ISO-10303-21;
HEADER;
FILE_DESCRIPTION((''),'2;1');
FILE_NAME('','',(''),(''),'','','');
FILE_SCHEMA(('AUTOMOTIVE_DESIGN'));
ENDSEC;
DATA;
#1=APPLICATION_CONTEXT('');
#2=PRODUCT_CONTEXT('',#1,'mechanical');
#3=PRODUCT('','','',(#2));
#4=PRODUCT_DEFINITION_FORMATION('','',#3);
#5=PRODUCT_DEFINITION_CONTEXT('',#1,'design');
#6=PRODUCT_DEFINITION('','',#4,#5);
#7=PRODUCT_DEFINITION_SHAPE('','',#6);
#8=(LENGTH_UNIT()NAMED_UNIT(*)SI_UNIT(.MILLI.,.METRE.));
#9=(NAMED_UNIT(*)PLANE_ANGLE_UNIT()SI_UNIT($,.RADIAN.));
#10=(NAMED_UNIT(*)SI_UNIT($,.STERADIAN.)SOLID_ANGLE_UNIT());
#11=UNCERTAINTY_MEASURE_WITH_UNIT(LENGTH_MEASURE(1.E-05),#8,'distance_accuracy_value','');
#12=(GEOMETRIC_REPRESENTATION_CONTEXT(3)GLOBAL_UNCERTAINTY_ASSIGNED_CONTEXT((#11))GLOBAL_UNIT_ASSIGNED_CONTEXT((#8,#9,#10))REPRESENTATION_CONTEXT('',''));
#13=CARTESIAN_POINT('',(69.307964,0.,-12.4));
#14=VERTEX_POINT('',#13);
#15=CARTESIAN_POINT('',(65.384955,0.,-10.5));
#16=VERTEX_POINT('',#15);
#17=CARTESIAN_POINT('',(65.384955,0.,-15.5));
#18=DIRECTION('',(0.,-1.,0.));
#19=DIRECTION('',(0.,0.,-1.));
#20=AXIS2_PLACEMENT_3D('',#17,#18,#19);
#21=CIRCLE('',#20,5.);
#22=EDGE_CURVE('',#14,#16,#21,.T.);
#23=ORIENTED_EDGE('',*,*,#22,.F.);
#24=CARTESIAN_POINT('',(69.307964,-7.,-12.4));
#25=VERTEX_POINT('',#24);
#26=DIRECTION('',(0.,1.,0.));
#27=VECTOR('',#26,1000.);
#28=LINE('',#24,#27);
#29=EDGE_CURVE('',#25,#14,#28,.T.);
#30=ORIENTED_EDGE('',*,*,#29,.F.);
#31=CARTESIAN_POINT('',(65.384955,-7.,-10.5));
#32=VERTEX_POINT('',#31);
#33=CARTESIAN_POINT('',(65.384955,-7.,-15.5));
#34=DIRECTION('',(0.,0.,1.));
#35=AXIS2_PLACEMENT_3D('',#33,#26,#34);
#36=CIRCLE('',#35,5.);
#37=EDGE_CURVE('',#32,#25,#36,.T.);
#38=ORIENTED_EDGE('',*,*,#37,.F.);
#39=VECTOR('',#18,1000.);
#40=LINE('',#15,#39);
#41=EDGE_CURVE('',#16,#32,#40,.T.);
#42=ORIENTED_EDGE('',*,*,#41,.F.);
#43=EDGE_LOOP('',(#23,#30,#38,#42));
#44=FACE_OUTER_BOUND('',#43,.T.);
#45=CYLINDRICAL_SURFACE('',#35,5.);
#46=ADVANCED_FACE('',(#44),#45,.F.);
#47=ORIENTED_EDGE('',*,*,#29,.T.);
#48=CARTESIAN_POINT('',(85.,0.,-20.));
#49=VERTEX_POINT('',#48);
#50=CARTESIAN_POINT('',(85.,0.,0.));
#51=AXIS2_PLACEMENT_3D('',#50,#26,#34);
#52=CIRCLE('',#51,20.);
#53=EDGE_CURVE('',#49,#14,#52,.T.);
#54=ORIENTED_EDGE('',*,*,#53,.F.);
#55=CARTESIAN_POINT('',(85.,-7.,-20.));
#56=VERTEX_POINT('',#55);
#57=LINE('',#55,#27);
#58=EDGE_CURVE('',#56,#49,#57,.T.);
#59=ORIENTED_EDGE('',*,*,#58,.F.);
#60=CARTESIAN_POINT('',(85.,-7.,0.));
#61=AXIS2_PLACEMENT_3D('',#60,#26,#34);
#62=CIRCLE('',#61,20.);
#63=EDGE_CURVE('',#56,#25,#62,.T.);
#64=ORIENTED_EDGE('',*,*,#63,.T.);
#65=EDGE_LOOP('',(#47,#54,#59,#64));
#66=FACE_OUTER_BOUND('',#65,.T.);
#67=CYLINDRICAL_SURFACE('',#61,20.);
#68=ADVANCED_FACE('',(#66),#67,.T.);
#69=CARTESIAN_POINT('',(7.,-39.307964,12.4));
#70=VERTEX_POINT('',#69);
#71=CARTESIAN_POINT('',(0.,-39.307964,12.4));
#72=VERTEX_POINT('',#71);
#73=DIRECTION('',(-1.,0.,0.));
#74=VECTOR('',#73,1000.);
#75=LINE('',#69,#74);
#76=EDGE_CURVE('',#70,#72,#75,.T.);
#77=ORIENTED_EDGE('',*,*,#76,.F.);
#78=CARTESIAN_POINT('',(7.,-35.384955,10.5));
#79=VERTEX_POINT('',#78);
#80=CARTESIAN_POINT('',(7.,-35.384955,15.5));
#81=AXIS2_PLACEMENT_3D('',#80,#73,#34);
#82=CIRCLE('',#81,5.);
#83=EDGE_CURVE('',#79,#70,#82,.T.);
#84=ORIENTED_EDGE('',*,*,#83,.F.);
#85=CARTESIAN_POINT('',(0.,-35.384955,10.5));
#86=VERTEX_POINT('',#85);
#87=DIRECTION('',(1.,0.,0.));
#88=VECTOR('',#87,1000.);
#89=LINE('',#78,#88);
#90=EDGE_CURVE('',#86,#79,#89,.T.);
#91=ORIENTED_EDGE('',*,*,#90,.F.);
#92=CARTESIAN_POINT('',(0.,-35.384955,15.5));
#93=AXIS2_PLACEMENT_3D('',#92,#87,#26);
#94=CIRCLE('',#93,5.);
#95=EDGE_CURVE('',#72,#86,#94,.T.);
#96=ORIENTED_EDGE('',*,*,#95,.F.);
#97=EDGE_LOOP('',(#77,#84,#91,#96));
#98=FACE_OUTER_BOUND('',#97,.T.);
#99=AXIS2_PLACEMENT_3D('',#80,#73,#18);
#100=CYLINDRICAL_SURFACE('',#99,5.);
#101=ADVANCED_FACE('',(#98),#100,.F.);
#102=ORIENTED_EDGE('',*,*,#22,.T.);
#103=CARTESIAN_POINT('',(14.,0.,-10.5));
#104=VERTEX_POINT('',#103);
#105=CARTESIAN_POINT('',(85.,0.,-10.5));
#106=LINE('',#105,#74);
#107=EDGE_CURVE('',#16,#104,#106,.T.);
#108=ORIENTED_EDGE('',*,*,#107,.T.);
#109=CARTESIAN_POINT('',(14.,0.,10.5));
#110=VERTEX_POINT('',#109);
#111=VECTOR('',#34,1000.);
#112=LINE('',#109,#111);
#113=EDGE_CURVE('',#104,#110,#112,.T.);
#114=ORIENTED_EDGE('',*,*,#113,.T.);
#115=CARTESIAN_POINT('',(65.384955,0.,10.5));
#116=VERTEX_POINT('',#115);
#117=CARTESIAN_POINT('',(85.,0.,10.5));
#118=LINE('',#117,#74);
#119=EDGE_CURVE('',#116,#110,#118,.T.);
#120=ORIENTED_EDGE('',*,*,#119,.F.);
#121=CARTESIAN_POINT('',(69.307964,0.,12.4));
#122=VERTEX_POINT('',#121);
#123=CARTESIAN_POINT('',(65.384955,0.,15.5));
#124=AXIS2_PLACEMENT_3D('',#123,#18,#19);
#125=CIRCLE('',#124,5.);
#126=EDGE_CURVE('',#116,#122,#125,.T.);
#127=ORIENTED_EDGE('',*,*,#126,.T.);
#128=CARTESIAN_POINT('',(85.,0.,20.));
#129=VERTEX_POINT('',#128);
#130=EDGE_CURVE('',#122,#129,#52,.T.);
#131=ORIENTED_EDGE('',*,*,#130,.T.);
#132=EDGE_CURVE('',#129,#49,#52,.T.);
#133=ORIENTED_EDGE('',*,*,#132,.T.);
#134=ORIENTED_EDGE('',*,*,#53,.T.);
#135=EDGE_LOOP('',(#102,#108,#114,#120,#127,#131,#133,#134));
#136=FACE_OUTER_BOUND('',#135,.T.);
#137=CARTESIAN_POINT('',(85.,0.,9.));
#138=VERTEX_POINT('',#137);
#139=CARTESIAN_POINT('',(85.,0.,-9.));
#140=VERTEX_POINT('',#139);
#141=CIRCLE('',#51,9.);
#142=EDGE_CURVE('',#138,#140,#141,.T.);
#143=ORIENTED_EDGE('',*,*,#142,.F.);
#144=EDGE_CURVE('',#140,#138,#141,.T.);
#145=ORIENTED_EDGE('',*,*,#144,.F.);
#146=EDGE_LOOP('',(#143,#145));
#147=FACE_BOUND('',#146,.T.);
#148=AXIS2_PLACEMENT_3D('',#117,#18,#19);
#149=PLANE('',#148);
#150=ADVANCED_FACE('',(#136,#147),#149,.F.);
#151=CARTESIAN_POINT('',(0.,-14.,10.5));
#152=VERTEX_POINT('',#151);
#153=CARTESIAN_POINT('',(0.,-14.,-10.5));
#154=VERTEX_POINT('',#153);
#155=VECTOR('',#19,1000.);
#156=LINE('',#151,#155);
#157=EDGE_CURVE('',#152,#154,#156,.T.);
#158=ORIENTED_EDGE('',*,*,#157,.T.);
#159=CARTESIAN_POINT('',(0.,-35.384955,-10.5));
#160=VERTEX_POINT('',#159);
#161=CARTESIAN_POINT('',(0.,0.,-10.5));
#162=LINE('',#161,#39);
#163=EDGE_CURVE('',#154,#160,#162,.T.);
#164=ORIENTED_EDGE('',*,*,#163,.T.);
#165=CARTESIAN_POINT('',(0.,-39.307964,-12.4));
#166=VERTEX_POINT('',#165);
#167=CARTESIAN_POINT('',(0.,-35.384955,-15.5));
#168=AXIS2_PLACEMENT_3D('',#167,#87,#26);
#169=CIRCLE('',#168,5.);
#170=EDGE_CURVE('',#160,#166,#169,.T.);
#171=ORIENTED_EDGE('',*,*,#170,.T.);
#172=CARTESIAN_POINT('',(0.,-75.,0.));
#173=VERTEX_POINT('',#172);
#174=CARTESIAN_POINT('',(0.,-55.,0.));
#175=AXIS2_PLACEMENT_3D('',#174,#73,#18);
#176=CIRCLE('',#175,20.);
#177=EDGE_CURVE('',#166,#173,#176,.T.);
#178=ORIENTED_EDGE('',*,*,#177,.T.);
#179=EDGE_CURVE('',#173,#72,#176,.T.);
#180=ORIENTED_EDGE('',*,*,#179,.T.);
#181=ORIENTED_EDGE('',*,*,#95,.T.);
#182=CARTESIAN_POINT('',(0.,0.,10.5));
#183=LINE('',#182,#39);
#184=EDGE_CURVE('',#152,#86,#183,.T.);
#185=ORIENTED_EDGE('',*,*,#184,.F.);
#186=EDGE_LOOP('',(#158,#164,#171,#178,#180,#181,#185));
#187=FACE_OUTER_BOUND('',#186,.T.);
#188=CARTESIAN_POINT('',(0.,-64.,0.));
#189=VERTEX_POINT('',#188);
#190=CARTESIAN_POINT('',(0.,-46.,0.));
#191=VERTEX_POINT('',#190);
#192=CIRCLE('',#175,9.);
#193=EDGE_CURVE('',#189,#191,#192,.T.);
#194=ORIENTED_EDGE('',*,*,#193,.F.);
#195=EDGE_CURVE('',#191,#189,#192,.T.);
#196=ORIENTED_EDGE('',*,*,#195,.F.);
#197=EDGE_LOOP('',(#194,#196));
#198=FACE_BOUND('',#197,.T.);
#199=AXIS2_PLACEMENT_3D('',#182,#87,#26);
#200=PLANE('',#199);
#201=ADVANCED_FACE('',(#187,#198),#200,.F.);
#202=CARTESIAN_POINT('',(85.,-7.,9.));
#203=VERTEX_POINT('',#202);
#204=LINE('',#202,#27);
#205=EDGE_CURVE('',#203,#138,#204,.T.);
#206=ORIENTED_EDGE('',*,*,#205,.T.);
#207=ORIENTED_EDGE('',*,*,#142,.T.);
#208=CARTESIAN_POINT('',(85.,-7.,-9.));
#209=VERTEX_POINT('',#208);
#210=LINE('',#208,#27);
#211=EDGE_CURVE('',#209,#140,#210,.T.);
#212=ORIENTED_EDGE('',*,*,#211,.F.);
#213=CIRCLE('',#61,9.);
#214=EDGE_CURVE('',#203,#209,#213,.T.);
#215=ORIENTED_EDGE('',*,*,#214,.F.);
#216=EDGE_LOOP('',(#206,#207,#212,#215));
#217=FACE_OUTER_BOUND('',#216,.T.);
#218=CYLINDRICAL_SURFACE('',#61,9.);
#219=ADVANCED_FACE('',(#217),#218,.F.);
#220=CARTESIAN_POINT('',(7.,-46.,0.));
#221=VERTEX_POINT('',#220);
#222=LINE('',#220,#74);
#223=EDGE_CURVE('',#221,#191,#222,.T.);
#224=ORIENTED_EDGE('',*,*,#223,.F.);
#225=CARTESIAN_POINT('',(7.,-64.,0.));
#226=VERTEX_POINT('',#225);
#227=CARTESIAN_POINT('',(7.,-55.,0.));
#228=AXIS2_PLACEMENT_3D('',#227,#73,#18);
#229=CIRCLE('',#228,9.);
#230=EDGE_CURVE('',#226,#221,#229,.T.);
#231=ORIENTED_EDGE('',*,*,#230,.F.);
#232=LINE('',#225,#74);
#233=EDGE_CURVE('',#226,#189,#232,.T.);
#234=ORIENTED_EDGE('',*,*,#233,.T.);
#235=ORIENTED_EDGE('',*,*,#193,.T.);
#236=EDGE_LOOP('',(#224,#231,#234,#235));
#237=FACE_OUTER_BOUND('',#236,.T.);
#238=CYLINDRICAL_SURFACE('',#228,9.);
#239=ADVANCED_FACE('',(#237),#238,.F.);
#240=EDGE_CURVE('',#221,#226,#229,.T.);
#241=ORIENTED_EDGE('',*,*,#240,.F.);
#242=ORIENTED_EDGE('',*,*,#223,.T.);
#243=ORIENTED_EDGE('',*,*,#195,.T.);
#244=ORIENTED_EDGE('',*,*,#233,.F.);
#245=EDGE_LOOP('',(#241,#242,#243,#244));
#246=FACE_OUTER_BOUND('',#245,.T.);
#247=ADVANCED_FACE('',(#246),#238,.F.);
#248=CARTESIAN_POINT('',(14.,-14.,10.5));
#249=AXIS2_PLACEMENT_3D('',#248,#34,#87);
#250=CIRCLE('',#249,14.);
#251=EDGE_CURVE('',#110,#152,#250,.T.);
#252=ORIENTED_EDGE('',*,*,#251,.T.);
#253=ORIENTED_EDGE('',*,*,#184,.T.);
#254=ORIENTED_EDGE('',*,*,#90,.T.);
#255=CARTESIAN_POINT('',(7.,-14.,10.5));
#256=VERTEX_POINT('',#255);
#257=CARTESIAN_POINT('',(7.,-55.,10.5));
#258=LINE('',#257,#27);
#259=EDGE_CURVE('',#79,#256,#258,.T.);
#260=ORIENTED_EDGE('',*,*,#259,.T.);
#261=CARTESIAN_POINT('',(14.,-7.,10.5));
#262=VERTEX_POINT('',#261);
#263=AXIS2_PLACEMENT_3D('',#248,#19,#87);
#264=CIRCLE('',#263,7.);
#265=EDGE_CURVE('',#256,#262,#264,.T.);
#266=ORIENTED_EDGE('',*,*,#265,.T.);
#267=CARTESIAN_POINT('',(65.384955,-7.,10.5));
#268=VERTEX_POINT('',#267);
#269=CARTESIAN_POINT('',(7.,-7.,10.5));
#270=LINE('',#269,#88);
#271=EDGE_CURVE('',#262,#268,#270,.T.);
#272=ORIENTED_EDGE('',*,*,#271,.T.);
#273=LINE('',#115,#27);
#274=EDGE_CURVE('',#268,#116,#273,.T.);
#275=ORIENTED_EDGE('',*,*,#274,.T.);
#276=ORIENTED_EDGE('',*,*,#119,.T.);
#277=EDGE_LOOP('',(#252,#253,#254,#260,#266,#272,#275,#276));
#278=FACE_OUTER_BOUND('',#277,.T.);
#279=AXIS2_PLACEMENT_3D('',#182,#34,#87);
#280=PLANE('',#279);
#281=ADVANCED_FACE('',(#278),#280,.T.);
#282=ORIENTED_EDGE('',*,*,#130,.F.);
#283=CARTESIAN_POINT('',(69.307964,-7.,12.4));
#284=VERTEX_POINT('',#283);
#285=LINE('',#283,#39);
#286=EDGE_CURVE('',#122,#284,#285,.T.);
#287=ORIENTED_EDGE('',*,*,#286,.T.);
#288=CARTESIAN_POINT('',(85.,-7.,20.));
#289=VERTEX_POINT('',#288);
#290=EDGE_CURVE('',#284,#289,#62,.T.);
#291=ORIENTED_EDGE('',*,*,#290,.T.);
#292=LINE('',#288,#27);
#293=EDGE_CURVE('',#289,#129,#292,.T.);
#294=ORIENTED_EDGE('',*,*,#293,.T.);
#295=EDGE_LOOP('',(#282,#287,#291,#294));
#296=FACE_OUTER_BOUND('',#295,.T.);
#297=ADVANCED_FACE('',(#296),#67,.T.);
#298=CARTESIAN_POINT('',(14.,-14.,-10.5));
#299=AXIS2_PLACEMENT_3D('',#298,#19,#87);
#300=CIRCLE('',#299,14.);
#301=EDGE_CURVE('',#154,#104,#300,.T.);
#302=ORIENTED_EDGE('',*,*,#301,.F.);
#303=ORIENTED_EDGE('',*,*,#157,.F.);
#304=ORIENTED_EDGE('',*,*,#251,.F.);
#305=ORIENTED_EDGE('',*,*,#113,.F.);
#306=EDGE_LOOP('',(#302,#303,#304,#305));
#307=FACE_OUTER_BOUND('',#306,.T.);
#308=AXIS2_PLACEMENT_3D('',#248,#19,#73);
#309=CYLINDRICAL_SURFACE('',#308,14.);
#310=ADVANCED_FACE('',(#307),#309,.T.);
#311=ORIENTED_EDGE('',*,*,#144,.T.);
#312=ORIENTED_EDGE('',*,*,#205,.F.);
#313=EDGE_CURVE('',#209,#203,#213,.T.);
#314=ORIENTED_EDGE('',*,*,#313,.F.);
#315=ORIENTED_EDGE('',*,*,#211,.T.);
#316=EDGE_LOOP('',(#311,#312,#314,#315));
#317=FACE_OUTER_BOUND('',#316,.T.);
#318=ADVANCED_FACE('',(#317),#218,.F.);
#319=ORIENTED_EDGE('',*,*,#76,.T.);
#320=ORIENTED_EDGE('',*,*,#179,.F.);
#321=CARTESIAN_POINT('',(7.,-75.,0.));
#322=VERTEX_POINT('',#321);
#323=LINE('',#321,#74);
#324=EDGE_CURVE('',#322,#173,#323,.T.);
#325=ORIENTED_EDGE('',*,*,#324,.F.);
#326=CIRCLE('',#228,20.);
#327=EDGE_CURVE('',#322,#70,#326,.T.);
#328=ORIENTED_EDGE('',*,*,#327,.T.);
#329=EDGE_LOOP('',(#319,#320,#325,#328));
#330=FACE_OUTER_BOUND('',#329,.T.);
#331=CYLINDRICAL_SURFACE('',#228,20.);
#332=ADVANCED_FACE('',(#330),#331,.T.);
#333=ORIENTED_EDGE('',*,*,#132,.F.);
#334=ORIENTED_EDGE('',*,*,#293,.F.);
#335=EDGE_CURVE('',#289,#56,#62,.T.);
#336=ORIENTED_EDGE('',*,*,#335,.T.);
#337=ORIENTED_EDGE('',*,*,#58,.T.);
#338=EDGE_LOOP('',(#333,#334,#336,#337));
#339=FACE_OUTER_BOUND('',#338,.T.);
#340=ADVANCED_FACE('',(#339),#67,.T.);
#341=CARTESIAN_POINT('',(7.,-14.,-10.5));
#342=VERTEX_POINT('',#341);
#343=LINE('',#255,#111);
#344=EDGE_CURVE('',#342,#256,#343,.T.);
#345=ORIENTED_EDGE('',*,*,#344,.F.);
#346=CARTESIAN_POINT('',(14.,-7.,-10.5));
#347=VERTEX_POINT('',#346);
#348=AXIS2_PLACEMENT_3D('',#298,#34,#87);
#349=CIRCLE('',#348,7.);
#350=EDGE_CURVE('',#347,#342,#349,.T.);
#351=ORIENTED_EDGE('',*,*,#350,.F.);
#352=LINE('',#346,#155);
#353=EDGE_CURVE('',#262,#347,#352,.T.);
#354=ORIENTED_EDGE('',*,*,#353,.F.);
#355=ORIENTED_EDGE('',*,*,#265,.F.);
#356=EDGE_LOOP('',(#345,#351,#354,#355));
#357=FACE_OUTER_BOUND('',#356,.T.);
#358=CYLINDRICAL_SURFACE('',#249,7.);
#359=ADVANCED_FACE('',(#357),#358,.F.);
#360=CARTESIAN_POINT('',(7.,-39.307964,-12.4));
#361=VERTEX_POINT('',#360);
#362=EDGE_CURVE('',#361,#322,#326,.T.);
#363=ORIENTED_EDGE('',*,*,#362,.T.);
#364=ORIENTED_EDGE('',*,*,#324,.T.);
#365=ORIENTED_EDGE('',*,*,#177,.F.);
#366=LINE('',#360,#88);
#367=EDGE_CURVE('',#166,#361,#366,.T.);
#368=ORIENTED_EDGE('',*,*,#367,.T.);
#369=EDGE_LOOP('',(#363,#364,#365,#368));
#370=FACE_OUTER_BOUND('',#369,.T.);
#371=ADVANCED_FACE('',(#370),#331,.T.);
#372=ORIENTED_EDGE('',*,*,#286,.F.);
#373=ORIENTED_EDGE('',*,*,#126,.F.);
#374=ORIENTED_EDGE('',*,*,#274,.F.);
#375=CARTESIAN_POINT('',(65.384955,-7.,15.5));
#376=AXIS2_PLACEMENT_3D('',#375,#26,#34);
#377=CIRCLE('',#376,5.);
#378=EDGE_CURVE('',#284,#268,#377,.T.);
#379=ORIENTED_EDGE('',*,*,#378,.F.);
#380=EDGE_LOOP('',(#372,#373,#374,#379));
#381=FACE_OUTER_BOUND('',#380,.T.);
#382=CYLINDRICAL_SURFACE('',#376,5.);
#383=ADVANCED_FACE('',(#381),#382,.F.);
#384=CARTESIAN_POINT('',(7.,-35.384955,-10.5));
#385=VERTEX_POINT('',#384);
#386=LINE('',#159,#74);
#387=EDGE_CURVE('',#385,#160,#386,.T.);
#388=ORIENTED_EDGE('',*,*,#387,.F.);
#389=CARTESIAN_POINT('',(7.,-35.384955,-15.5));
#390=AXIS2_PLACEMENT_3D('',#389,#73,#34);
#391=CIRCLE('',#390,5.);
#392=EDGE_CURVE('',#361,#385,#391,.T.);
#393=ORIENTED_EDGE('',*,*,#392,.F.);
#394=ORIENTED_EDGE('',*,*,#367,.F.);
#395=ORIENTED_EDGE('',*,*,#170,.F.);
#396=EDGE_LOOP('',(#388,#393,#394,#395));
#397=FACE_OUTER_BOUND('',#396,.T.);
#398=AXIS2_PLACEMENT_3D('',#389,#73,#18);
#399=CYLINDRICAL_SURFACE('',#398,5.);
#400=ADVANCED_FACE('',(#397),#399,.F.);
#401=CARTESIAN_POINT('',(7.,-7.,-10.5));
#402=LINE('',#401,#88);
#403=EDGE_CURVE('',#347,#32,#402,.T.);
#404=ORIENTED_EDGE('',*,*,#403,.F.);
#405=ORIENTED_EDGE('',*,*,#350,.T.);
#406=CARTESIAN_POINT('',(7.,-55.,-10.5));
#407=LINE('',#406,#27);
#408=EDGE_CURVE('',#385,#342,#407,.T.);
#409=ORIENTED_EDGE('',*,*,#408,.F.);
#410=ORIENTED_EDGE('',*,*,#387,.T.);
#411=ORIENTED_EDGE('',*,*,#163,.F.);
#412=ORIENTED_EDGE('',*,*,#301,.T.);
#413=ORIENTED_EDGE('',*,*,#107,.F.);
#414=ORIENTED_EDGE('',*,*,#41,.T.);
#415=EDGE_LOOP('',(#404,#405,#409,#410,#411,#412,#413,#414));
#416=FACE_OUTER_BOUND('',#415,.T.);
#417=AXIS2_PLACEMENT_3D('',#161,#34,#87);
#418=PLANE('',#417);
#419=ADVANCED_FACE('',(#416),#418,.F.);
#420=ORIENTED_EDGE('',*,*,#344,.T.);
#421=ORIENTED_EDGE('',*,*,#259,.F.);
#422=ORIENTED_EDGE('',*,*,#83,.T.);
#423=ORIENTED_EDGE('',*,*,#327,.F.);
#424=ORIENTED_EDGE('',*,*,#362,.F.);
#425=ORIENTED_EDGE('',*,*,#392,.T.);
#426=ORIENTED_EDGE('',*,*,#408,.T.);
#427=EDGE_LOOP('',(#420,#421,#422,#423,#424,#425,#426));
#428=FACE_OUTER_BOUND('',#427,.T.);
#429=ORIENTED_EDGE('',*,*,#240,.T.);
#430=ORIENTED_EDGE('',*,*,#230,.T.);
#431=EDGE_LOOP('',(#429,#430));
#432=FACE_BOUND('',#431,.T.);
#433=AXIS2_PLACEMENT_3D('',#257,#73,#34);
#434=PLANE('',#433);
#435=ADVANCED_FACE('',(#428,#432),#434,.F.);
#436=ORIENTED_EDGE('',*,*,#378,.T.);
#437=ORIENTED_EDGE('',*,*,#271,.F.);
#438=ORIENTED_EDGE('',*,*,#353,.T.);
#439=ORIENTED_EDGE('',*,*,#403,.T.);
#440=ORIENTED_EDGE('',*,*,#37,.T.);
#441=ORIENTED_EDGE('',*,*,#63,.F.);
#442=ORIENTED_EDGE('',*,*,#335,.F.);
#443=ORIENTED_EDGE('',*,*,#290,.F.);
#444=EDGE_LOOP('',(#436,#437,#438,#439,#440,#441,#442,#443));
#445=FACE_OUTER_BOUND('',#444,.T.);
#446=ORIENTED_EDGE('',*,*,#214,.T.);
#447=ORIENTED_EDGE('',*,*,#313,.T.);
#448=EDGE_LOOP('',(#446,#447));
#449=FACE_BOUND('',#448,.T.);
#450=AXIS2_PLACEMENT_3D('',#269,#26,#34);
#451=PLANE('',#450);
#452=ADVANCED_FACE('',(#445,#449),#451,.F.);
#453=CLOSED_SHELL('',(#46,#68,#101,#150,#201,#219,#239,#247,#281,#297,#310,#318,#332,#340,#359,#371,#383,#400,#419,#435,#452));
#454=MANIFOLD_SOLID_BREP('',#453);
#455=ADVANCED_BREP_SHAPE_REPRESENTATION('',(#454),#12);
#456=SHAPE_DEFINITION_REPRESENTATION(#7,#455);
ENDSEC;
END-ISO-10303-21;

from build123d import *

# Parameters (mm, degrees)
L_STRIP_BODY_DEPTH         = 10.5
EYE_LUG_A_SKETCH_R         = 20
EYE_LUG_A_40_DEPTH         = 7
EYE_HOLE_A_18_DEPTH        = 7
EYE_LUG_B_SKETCH_R         = 20
EYE_LUG_B_SKETCH_R_2       = 9
EYE_LUG_B_40_DEPTH         = 7
EYE_HOLE_B_18_DEPTH        = 7
OUTER_BEND_FILLET_R14_R    = 14
INNER_BEND_FILLET_R7_R     = 7
EYE_LUG_BLEND_FILLETS_R5_R = 5


with BuildPart() as part:
    # L Strip Profile Sketch → L Strip Body (new, symmetric)
    with BuildSketch(Plane.XY):
        Polygon((85, 0), (0, 0), (0, -55), (7, -55), (7, -7), (85, -7), align=None)
    extrude(amount=L_STRIP_BODY_DEPTH, both=True)

    # Eye Lug A Sketch → Eye Lug A _40 (add)
    with BuildSketch(Plane(origin=(0, 0, 0), x_dir=(1, 0, 0), z_dir=(0, 1, 0))):
        with Locations((85, 0)):
            Circle(EYE_LUG_A_SKETCH_R)
    extrude(amount=-EYE_LUG_A_40_DEPTH)

    # Sketch2_3 → Eye Hole A _18 (cut)
    with BuildSketch(Plane(origin=(0, 0, 0), x_dir=(1, 0, 0), z_dir=(0, 1, 0))):
        with BuildLine():
            Line((85, 9), (85, -9))
            ThreePointArc((85, -9), (91.363961031, -6.363961031), (94, 0))
            ThreePointArc((94, 0), (91.363961031, 6.363961031), (85, 9))
        make_face()
        with BuildLine():
            ThreePointArc((85, 9), (76, 0), (85, -9))
            Line((85, -9), (85, 9))
        make_face()
        with BuildLine():
            Line((85, 9), (85, -9))
            ThreePointArc((85, -9), (91.363961031, -6.363961031), (94, 0))
            ThreePointArc((94, 0), (91.363961031, 6.363961031), (85, 9))
        make_face()
        with BuildLine():
            ThreePointArc((85, 9), (76, 0), (85, -9))
            Line((85, -9), (85, 9))
        make_face()
    extrude(amount=-EYE_HOLE_A_18_DEPTH, mode=Mode.SUBTRACT)

    # Eye Lug B Sketch → Eye Lug B _40 (add)
    with BuildSketch(Plane.ZY):
        with Locations((0, -55)):
            Circle(EYE_LUG_B_SKETCH_R)
        with Locations((0, -55)):
            Circle(EYE_LUG_B_SKETCH_R_2, mode=Mode.SUBTRACT)
    extrude(amount=-EYE_LUG_B_40_DEPTH)

    # Sketch4_2 → Eye Hole B _18 (cut)
    with BuildSketch(Plane.ZY):
        with BuildLine():
            Line((-9, -55), (9, -55))
            ThreePointArc((9, -55), (0, -46), (-9, -55))
        make_face()
        with BuildLine():
            ThreePointArc((-9, -55), (0, -64), (9, -55))
            Line((9, -55), (-9, -55))
        make_face()
    extrude(amount=-EYE_HOLE_B_18_DEPTH, mode=Mode.SUBTRACT)

    # Outer Bend Fillet R14
    outer_bend_fillet_r14_edges = [part.edges().sort_by_distance(p)[0] for p in [
        (0, 0, 0),
    ]]
    fillet(outer_bend_fillet_r14_edges, radius=OUTER_BEND_FILLET_R14_R)

    # Inner Bend Fillet R7
    inner_bend_fillet_r7_edges = [part.edges().sort_by_distance(p)[0] for p in [
        (7, -7, 0),
    ]]
    fillet(inner_bend_fillet_r7_edges, radius=INNER_BEND_FILLET_R7_R)

    # Eye Lug Blend Fillets R5
    eye_lug_blend_fillets_r5_edges = [part.edges().sort_by_distance(p)[0] for p in [
        (67.977955469, -3.5, 10.5),
        (67.977955469, -3.5, -10.5),
        (3.5, -37.977955469, -10.5),
        (3.5, -37.977955469, 10.5),
    ]]
    fillet(eye_lug_blend_fillets_r5_edges, radius=EYE_LUG_BLEND_FILLETS_R5_R)


solid = part.part
